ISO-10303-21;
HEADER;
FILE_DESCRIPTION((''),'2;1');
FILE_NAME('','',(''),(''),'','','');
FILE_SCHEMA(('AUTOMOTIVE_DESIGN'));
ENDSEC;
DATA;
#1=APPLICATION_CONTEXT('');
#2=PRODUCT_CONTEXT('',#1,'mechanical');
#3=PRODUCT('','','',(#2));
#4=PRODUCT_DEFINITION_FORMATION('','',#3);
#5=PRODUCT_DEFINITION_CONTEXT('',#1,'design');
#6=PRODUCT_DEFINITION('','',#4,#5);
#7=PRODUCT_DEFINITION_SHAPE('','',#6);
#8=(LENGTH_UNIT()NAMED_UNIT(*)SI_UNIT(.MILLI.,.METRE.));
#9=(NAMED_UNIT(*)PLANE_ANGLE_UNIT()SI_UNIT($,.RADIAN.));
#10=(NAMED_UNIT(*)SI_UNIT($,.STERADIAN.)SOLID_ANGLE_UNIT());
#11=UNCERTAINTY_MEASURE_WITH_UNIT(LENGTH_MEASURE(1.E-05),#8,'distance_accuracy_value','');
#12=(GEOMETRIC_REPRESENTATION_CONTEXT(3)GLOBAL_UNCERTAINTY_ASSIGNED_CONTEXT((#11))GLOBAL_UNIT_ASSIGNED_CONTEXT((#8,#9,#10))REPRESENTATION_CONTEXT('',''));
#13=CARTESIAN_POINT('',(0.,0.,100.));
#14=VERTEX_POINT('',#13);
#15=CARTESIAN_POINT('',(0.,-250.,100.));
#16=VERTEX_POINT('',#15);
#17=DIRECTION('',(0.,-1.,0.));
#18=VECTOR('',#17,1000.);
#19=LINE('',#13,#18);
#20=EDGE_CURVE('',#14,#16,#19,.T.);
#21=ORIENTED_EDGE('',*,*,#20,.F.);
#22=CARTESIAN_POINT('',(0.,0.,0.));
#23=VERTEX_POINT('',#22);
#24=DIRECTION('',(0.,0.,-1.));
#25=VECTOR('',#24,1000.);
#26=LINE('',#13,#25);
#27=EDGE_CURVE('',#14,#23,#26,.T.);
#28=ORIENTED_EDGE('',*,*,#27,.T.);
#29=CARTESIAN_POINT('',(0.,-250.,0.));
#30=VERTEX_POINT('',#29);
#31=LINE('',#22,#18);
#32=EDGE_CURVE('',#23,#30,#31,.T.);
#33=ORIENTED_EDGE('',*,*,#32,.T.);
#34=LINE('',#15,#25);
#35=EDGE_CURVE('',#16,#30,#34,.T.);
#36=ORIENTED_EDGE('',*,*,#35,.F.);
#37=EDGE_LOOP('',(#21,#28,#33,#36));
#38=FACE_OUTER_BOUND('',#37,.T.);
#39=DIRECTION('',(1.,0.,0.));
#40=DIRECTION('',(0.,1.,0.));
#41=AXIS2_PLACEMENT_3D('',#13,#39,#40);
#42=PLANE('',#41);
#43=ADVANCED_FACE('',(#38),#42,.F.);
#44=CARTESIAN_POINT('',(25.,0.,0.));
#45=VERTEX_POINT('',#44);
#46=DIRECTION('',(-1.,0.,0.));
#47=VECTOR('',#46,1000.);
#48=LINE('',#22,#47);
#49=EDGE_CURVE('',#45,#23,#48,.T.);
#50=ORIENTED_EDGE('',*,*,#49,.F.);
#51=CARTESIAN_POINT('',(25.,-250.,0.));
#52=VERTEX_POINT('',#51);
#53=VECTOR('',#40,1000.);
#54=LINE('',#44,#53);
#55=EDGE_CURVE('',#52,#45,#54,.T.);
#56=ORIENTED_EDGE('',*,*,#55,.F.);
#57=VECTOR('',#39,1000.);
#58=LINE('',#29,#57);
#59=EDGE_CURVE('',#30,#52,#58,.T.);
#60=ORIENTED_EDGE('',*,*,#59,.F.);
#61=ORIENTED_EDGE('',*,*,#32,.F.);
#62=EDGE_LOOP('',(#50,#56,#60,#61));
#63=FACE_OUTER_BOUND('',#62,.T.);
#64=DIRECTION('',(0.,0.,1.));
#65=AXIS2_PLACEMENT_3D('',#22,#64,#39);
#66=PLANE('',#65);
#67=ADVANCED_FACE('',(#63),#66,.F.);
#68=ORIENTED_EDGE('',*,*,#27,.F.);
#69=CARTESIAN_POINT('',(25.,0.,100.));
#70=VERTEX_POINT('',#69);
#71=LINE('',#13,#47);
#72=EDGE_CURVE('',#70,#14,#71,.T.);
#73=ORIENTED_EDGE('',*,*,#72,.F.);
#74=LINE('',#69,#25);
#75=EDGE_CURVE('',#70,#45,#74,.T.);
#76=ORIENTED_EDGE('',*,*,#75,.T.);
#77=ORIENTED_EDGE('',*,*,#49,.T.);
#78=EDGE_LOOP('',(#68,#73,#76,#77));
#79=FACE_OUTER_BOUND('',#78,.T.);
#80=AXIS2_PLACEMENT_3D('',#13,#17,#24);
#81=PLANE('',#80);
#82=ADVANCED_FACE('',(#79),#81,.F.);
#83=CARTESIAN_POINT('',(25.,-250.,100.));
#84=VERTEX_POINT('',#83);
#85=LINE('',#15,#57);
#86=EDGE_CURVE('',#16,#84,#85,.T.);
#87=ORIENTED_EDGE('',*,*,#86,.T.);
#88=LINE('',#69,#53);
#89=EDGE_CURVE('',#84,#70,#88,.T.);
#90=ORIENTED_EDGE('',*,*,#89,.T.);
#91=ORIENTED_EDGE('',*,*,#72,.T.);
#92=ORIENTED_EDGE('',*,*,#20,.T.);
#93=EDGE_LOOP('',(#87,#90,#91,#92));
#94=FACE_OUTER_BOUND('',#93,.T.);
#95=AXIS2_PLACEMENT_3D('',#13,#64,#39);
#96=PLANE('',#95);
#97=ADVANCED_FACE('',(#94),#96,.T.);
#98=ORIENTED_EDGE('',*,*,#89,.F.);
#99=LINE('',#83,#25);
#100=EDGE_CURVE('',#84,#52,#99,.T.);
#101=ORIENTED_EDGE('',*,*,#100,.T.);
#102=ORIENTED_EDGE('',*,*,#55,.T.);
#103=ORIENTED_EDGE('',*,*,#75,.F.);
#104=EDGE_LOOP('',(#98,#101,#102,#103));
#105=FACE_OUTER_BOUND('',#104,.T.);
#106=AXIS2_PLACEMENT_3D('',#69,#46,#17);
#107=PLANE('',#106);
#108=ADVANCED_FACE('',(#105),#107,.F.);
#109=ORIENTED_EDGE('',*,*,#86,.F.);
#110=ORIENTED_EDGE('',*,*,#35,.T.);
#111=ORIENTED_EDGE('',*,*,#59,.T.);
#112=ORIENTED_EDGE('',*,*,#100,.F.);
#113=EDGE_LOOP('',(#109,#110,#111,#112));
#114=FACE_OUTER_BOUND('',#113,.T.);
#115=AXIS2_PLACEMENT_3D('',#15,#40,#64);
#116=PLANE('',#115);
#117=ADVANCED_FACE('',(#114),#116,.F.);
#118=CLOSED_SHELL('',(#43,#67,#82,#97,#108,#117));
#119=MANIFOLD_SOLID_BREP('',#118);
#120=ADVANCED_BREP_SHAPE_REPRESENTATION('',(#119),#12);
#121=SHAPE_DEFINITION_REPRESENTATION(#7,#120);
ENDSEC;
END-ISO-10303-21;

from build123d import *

# Parameters (mm, degrees)
SKETCH1_W           = 25
SKETCH1_H           = 250
BOSS_EXTRUDE1_DEPTH = 100


with BuildPart() as part:
    # Sketch1 → Boss-Extrude1 (new body)
    with BuildSketch(Plane.XY):
        with Locations((12.5, -125)):
            Rectangle(SKETCH1_W, SKETCH1_H)
    extrude(amount=BOSS_EXTRUDE1_DEPTH)


solid = part.part
